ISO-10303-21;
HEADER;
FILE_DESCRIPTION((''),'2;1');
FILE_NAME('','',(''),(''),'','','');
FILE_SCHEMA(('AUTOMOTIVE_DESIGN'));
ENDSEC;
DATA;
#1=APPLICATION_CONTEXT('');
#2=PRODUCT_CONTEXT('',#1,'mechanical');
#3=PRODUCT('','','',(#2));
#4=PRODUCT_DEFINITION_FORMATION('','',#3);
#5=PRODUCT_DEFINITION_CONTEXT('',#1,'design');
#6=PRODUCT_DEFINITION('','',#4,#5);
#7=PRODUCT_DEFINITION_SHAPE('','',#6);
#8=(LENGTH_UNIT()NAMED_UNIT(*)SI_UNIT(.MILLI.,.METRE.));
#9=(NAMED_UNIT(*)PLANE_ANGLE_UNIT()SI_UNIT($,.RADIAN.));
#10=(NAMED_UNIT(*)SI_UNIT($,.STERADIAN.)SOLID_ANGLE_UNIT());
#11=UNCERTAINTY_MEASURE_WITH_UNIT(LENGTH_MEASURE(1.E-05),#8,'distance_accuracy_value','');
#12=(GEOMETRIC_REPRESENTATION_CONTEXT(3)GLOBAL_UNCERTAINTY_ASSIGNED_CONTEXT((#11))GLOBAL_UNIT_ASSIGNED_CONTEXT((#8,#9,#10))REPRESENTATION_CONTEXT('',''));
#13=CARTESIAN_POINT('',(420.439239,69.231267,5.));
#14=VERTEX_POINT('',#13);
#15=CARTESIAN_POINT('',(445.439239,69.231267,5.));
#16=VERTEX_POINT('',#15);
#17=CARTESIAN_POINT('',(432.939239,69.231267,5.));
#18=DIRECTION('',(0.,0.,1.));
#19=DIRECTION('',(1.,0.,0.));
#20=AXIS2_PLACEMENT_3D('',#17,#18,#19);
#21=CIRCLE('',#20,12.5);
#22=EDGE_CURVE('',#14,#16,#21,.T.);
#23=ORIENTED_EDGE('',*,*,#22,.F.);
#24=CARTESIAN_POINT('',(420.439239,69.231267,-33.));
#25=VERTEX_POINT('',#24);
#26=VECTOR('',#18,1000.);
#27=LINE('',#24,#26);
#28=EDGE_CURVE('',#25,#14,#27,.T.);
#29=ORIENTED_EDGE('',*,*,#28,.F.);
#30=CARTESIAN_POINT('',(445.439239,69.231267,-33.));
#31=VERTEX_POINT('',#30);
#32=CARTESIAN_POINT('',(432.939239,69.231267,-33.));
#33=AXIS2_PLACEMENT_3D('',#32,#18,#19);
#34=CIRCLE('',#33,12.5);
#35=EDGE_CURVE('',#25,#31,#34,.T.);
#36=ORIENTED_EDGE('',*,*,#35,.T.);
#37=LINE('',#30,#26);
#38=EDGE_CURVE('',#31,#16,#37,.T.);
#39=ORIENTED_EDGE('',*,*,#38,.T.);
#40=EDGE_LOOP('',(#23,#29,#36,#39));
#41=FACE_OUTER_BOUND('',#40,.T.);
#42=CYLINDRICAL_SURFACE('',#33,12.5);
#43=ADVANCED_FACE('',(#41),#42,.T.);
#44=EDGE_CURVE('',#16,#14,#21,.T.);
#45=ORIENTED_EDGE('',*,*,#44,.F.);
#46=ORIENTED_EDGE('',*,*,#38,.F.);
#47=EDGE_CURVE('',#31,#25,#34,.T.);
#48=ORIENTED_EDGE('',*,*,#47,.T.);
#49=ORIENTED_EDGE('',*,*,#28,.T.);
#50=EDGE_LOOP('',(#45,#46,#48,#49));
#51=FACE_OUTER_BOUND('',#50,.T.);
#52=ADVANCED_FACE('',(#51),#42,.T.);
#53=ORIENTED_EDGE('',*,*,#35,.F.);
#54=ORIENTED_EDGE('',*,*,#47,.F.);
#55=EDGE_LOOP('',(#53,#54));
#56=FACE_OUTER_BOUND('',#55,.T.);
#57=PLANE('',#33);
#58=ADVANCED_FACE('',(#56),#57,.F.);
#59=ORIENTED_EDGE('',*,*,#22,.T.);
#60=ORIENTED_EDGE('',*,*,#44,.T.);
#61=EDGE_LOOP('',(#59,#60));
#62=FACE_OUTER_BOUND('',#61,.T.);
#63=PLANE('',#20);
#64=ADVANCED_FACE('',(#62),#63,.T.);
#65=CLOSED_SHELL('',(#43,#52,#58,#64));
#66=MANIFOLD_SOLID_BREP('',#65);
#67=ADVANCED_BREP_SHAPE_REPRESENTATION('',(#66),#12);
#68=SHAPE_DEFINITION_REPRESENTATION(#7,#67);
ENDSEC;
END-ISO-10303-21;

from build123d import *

# Parameters (mm, degrees)
BOSS_EXTRUDE1_DEPTH      = 5
BOSS_EXTRUDE1_DEPTH_BACK = 33
SKETCH1_R                = 12.5


with BuildPart() as part:
    # Sketch1 → Boss-Extrude1 (new, two sides: drawn at the far end of the back side and taken through both)
    with BuildSketch(Plane.XY.offset(-BOSS_EXTRUDE1_DEPTH_BACK)):
        with Locations((432.939239469, 69.231267182)):
            Circle(SKETCH1_R)
    extrude(amount=BOSS_EXTRUDE1_DEPTH + BOSS_EXTRUDE1_DEPTH_BACK)


solid = part.part
